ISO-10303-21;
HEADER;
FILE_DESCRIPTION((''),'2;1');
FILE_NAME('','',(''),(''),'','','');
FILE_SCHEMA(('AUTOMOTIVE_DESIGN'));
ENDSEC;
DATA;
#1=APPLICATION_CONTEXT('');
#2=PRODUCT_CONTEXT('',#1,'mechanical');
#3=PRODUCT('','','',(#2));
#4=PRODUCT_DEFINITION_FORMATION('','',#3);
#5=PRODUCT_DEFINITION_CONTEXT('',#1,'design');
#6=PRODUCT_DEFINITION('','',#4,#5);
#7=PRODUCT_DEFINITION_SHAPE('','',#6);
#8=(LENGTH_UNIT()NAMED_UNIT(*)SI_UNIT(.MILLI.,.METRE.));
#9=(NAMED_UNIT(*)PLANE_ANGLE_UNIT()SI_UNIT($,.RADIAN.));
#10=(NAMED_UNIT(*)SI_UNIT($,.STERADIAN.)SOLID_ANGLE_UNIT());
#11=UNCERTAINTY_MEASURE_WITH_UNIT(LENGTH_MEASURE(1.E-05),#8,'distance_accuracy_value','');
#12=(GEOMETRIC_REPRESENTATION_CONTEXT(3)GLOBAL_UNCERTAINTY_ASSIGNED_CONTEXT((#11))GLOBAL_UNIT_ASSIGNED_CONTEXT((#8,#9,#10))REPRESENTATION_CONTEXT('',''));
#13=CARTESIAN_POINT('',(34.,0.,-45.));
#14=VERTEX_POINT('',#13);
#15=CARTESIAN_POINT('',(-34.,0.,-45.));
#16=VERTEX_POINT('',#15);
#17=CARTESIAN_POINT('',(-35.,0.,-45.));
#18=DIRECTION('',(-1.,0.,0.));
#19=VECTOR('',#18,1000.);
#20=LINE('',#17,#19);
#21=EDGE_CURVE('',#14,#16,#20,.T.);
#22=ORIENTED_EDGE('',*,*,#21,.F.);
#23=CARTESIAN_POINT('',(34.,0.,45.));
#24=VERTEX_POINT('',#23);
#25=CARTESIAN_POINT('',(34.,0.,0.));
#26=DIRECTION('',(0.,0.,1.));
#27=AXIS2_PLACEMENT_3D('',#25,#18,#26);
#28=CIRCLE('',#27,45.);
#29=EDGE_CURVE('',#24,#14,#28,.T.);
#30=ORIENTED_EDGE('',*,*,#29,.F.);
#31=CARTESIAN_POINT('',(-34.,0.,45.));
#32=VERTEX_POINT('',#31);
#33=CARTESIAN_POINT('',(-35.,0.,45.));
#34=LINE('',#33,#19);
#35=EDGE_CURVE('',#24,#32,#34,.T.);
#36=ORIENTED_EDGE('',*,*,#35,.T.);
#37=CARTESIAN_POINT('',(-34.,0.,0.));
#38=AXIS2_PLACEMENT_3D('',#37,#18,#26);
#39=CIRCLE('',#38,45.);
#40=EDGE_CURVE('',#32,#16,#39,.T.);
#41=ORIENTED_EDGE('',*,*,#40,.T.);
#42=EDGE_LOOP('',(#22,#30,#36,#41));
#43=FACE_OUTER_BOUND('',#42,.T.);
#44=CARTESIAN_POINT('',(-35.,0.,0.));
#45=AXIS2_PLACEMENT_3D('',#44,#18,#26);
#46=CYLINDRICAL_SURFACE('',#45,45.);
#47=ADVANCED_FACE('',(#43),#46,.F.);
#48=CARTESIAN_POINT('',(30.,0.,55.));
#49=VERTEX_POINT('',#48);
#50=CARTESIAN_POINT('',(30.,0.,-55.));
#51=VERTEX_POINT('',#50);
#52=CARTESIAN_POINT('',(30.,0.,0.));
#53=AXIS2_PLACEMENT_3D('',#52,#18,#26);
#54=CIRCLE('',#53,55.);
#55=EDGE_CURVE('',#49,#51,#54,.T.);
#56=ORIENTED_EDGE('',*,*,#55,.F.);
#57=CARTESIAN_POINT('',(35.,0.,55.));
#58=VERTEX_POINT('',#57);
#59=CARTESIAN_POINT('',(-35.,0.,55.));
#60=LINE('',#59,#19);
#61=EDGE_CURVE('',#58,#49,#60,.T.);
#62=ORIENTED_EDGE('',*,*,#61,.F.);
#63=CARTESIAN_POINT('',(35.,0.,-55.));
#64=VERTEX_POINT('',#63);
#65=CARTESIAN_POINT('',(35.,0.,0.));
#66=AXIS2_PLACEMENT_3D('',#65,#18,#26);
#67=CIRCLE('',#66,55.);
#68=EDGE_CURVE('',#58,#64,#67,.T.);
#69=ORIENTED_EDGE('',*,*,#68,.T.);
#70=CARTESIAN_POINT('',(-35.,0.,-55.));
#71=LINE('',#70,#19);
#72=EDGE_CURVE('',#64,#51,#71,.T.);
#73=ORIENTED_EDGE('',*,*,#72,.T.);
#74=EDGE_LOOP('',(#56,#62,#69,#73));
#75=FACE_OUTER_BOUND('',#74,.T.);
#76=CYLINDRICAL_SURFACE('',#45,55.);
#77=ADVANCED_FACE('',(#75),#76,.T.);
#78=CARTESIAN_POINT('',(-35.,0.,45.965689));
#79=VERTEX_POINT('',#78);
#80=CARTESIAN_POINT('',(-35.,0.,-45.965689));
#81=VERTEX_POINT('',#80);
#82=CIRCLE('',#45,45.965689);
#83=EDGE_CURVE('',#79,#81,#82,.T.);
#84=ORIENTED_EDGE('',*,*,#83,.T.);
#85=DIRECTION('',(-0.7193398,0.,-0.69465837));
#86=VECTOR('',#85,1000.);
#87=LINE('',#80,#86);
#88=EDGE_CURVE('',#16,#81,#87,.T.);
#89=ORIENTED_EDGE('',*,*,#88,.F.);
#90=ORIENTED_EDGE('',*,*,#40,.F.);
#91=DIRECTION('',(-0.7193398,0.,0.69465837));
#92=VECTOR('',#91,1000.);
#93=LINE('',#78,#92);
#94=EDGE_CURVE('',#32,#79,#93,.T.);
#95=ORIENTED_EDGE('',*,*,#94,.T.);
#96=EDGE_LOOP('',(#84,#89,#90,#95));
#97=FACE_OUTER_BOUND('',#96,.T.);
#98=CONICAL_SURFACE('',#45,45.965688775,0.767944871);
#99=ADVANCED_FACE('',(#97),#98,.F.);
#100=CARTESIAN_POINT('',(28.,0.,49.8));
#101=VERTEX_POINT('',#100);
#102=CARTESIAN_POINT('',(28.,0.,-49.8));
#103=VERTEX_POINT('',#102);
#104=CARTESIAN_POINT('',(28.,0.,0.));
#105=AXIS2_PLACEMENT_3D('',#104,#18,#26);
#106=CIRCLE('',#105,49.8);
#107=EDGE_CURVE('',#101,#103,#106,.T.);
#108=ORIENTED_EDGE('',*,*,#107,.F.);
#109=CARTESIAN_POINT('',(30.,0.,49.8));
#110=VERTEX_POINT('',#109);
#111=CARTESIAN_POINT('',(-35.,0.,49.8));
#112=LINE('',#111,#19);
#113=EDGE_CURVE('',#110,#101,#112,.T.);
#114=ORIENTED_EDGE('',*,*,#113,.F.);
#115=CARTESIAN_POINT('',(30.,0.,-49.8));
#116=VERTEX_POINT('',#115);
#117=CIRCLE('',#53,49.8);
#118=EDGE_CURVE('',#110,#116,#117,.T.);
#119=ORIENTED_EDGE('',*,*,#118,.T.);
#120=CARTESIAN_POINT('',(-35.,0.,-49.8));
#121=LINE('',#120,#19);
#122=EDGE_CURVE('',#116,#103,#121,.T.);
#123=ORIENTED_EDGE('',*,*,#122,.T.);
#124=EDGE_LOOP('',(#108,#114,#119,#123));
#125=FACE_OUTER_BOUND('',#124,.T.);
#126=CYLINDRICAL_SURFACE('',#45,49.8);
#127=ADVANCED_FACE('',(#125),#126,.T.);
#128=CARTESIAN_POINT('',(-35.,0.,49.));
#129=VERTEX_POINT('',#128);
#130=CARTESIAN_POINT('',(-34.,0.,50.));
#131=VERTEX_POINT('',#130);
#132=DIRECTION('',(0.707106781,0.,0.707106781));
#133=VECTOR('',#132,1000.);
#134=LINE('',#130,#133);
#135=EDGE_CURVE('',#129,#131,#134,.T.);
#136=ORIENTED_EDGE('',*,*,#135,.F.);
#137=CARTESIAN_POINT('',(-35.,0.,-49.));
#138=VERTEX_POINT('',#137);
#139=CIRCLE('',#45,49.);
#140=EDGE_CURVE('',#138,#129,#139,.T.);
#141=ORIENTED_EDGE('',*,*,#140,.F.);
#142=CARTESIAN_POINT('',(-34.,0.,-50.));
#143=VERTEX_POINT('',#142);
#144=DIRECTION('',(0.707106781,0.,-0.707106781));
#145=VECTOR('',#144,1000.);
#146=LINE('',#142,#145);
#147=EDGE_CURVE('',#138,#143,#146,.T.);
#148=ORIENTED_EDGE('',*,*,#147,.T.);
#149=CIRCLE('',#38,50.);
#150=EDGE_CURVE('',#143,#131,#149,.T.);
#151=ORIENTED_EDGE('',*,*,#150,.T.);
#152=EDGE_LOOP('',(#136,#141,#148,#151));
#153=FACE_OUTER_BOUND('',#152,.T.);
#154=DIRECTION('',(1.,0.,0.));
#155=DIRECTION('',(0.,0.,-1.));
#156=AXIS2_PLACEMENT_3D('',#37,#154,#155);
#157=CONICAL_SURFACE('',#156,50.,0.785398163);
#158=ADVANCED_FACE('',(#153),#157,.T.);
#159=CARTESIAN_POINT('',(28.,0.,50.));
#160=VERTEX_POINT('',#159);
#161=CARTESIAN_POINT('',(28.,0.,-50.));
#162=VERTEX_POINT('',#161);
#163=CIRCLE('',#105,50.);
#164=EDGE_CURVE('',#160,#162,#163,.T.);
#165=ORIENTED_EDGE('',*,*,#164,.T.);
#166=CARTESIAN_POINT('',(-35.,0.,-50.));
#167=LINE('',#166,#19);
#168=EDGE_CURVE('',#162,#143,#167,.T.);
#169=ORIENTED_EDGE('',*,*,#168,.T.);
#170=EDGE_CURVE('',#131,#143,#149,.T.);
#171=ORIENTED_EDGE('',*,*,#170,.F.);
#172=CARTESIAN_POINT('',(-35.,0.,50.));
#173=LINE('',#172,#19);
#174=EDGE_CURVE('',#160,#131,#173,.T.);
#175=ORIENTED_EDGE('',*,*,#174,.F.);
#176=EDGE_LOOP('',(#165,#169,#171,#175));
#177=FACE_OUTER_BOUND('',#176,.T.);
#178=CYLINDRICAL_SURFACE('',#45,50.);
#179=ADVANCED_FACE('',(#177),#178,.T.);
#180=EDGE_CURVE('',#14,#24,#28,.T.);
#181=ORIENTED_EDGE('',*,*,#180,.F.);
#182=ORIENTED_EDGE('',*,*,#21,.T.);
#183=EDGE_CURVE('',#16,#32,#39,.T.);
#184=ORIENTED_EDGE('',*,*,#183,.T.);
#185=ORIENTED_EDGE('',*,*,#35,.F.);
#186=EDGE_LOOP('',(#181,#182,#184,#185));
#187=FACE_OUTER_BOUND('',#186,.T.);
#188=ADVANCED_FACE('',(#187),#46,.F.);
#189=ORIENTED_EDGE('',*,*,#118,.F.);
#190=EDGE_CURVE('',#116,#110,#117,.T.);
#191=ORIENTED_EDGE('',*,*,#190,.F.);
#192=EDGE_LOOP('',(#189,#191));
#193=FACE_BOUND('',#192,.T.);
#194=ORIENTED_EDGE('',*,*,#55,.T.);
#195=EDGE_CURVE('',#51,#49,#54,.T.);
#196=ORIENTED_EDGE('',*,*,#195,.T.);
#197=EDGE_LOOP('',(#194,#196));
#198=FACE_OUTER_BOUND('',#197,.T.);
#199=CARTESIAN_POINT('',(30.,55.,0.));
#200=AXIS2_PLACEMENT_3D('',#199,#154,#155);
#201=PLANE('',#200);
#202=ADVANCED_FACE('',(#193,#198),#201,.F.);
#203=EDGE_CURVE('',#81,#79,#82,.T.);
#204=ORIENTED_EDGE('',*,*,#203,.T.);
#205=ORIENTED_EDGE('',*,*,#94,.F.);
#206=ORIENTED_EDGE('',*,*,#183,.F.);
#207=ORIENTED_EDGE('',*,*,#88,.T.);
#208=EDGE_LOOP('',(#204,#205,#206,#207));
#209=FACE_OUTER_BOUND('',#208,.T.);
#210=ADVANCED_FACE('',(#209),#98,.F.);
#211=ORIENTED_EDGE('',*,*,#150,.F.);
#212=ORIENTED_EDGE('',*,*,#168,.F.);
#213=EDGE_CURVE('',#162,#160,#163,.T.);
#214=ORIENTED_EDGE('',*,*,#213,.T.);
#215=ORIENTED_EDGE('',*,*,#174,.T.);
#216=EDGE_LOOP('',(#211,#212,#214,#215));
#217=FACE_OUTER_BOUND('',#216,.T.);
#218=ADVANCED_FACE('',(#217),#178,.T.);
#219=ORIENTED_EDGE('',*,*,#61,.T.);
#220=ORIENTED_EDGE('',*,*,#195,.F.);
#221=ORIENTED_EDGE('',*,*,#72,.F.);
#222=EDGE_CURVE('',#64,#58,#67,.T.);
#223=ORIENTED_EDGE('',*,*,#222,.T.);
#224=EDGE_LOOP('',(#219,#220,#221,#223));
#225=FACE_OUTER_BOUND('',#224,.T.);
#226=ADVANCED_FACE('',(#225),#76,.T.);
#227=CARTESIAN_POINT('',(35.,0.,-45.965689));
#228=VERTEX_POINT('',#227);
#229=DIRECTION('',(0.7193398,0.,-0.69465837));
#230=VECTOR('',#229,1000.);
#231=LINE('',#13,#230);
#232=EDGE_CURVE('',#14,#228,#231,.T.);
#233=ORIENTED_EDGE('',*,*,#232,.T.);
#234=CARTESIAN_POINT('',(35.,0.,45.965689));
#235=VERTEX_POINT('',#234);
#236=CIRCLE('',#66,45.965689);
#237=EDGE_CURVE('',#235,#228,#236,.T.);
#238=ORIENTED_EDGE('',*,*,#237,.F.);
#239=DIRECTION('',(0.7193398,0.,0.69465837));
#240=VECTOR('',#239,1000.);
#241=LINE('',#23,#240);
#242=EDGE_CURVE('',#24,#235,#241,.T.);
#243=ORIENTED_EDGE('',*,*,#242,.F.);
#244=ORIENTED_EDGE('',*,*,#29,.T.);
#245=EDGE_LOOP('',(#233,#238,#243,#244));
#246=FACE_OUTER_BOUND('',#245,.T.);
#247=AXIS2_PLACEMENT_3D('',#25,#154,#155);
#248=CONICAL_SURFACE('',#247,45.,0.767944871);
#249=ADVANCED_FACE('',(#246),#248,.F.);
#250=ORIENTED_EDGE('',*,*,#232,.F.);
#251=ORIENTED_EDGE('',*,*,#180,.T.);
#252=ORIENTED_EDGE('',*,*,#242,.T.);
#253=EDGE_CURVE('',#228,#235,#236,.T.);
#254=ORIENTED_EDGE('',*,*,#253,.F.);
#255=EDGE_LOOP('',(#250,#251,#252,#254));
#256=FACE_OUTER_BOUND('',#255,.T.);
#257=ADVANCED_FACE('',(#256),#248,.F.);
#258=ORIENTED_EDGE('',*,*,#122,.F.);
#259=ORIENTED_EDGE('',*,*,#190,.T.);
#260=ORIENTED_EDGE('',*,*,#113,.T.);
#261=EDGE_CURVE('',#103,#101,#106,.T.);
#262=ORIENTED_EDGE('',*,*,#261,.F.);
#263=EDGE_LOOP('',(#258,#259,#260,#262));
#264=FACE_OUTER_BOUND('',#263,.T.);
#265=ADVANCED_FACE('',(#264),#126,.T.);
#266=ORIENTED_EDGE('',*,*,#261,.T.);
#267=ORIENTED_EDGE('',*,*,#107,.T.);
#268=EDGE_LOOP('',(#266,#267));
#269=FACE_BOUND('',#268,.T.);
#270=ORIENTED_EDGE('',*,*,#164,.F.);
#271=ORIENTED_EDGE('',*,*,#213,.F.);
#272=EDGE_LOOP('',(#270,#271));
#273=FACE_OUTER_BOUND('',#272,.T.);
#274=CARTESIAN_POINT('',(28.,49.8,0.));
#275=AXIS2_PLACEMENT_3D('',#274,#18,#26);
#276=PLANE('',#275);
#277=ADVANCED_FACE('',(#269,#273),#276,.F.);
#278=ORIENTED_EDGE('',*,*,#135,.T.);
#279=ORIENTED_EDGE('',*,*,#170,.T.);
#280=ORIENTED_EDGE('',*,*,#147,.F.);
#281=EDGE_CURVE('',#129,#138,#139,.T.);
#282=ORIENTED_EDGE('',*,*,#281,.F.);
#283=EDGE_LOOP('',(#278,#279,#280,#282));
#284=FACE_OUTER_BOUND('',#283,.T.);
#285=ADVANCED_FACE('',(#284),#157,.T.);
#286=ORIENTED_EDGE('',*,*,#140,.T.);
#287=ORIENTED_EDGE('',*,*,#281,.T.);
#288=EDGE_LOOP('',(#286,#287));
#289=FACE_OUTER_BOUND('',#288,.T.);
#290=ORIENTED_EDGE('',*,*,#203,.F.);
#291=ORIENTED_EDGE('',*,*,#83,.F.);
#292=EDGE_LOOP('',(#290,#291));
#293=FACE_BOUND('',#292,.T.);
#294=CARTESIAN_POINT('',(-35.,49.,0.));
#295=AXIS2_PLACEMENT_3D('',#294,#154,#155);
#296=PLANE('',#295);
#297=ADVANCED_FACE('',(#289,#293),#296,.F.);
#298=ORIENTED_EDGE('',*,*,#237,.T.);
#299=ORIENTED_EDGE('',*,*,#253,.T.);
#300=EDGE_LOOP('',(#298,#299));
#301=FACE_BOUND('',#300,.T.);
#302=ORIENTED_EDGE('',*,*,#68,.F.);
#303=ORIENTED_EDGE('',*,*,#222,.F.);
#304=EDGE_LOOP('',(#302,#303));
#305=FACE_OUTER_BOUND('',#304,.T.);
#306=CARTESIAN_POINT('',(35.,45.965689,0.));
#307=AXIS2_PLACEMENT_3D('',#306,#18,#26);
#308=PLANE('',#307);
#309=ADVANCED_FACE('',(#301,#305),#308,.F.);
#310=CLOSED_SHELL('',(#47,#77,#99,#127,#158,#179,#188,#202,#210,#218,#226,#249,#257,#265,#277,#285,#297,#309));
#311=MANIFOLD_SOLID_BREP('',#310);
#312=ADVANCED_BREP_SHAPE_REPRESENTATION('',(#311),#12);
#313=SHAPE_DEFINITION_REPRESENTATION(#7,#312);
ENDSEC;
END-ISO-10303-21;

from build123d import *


with BuildPart() as part:
    # Sketch 181 → 旋转1 (revolve)
    with BuildSketch(Plane.XY, mode=Mode.PRIVATE) as revolve_1_sk:
        Polygon((-35, 45.965688775), (-34, 45), (34, 45), (35, 45.965688775), (35, 55), (30, 55), (30, 49.8), (28, 49.8), (28, 50), (-34, 50), (-35, 49), align=None)
    revolve(revolve_1_sk.sketch.rotate(Axis((-35, 0, 0), (1, 0, 0)), 90), axis=Axis((-35, 0, 0), (1, 0, 0)))


solid = part.part
